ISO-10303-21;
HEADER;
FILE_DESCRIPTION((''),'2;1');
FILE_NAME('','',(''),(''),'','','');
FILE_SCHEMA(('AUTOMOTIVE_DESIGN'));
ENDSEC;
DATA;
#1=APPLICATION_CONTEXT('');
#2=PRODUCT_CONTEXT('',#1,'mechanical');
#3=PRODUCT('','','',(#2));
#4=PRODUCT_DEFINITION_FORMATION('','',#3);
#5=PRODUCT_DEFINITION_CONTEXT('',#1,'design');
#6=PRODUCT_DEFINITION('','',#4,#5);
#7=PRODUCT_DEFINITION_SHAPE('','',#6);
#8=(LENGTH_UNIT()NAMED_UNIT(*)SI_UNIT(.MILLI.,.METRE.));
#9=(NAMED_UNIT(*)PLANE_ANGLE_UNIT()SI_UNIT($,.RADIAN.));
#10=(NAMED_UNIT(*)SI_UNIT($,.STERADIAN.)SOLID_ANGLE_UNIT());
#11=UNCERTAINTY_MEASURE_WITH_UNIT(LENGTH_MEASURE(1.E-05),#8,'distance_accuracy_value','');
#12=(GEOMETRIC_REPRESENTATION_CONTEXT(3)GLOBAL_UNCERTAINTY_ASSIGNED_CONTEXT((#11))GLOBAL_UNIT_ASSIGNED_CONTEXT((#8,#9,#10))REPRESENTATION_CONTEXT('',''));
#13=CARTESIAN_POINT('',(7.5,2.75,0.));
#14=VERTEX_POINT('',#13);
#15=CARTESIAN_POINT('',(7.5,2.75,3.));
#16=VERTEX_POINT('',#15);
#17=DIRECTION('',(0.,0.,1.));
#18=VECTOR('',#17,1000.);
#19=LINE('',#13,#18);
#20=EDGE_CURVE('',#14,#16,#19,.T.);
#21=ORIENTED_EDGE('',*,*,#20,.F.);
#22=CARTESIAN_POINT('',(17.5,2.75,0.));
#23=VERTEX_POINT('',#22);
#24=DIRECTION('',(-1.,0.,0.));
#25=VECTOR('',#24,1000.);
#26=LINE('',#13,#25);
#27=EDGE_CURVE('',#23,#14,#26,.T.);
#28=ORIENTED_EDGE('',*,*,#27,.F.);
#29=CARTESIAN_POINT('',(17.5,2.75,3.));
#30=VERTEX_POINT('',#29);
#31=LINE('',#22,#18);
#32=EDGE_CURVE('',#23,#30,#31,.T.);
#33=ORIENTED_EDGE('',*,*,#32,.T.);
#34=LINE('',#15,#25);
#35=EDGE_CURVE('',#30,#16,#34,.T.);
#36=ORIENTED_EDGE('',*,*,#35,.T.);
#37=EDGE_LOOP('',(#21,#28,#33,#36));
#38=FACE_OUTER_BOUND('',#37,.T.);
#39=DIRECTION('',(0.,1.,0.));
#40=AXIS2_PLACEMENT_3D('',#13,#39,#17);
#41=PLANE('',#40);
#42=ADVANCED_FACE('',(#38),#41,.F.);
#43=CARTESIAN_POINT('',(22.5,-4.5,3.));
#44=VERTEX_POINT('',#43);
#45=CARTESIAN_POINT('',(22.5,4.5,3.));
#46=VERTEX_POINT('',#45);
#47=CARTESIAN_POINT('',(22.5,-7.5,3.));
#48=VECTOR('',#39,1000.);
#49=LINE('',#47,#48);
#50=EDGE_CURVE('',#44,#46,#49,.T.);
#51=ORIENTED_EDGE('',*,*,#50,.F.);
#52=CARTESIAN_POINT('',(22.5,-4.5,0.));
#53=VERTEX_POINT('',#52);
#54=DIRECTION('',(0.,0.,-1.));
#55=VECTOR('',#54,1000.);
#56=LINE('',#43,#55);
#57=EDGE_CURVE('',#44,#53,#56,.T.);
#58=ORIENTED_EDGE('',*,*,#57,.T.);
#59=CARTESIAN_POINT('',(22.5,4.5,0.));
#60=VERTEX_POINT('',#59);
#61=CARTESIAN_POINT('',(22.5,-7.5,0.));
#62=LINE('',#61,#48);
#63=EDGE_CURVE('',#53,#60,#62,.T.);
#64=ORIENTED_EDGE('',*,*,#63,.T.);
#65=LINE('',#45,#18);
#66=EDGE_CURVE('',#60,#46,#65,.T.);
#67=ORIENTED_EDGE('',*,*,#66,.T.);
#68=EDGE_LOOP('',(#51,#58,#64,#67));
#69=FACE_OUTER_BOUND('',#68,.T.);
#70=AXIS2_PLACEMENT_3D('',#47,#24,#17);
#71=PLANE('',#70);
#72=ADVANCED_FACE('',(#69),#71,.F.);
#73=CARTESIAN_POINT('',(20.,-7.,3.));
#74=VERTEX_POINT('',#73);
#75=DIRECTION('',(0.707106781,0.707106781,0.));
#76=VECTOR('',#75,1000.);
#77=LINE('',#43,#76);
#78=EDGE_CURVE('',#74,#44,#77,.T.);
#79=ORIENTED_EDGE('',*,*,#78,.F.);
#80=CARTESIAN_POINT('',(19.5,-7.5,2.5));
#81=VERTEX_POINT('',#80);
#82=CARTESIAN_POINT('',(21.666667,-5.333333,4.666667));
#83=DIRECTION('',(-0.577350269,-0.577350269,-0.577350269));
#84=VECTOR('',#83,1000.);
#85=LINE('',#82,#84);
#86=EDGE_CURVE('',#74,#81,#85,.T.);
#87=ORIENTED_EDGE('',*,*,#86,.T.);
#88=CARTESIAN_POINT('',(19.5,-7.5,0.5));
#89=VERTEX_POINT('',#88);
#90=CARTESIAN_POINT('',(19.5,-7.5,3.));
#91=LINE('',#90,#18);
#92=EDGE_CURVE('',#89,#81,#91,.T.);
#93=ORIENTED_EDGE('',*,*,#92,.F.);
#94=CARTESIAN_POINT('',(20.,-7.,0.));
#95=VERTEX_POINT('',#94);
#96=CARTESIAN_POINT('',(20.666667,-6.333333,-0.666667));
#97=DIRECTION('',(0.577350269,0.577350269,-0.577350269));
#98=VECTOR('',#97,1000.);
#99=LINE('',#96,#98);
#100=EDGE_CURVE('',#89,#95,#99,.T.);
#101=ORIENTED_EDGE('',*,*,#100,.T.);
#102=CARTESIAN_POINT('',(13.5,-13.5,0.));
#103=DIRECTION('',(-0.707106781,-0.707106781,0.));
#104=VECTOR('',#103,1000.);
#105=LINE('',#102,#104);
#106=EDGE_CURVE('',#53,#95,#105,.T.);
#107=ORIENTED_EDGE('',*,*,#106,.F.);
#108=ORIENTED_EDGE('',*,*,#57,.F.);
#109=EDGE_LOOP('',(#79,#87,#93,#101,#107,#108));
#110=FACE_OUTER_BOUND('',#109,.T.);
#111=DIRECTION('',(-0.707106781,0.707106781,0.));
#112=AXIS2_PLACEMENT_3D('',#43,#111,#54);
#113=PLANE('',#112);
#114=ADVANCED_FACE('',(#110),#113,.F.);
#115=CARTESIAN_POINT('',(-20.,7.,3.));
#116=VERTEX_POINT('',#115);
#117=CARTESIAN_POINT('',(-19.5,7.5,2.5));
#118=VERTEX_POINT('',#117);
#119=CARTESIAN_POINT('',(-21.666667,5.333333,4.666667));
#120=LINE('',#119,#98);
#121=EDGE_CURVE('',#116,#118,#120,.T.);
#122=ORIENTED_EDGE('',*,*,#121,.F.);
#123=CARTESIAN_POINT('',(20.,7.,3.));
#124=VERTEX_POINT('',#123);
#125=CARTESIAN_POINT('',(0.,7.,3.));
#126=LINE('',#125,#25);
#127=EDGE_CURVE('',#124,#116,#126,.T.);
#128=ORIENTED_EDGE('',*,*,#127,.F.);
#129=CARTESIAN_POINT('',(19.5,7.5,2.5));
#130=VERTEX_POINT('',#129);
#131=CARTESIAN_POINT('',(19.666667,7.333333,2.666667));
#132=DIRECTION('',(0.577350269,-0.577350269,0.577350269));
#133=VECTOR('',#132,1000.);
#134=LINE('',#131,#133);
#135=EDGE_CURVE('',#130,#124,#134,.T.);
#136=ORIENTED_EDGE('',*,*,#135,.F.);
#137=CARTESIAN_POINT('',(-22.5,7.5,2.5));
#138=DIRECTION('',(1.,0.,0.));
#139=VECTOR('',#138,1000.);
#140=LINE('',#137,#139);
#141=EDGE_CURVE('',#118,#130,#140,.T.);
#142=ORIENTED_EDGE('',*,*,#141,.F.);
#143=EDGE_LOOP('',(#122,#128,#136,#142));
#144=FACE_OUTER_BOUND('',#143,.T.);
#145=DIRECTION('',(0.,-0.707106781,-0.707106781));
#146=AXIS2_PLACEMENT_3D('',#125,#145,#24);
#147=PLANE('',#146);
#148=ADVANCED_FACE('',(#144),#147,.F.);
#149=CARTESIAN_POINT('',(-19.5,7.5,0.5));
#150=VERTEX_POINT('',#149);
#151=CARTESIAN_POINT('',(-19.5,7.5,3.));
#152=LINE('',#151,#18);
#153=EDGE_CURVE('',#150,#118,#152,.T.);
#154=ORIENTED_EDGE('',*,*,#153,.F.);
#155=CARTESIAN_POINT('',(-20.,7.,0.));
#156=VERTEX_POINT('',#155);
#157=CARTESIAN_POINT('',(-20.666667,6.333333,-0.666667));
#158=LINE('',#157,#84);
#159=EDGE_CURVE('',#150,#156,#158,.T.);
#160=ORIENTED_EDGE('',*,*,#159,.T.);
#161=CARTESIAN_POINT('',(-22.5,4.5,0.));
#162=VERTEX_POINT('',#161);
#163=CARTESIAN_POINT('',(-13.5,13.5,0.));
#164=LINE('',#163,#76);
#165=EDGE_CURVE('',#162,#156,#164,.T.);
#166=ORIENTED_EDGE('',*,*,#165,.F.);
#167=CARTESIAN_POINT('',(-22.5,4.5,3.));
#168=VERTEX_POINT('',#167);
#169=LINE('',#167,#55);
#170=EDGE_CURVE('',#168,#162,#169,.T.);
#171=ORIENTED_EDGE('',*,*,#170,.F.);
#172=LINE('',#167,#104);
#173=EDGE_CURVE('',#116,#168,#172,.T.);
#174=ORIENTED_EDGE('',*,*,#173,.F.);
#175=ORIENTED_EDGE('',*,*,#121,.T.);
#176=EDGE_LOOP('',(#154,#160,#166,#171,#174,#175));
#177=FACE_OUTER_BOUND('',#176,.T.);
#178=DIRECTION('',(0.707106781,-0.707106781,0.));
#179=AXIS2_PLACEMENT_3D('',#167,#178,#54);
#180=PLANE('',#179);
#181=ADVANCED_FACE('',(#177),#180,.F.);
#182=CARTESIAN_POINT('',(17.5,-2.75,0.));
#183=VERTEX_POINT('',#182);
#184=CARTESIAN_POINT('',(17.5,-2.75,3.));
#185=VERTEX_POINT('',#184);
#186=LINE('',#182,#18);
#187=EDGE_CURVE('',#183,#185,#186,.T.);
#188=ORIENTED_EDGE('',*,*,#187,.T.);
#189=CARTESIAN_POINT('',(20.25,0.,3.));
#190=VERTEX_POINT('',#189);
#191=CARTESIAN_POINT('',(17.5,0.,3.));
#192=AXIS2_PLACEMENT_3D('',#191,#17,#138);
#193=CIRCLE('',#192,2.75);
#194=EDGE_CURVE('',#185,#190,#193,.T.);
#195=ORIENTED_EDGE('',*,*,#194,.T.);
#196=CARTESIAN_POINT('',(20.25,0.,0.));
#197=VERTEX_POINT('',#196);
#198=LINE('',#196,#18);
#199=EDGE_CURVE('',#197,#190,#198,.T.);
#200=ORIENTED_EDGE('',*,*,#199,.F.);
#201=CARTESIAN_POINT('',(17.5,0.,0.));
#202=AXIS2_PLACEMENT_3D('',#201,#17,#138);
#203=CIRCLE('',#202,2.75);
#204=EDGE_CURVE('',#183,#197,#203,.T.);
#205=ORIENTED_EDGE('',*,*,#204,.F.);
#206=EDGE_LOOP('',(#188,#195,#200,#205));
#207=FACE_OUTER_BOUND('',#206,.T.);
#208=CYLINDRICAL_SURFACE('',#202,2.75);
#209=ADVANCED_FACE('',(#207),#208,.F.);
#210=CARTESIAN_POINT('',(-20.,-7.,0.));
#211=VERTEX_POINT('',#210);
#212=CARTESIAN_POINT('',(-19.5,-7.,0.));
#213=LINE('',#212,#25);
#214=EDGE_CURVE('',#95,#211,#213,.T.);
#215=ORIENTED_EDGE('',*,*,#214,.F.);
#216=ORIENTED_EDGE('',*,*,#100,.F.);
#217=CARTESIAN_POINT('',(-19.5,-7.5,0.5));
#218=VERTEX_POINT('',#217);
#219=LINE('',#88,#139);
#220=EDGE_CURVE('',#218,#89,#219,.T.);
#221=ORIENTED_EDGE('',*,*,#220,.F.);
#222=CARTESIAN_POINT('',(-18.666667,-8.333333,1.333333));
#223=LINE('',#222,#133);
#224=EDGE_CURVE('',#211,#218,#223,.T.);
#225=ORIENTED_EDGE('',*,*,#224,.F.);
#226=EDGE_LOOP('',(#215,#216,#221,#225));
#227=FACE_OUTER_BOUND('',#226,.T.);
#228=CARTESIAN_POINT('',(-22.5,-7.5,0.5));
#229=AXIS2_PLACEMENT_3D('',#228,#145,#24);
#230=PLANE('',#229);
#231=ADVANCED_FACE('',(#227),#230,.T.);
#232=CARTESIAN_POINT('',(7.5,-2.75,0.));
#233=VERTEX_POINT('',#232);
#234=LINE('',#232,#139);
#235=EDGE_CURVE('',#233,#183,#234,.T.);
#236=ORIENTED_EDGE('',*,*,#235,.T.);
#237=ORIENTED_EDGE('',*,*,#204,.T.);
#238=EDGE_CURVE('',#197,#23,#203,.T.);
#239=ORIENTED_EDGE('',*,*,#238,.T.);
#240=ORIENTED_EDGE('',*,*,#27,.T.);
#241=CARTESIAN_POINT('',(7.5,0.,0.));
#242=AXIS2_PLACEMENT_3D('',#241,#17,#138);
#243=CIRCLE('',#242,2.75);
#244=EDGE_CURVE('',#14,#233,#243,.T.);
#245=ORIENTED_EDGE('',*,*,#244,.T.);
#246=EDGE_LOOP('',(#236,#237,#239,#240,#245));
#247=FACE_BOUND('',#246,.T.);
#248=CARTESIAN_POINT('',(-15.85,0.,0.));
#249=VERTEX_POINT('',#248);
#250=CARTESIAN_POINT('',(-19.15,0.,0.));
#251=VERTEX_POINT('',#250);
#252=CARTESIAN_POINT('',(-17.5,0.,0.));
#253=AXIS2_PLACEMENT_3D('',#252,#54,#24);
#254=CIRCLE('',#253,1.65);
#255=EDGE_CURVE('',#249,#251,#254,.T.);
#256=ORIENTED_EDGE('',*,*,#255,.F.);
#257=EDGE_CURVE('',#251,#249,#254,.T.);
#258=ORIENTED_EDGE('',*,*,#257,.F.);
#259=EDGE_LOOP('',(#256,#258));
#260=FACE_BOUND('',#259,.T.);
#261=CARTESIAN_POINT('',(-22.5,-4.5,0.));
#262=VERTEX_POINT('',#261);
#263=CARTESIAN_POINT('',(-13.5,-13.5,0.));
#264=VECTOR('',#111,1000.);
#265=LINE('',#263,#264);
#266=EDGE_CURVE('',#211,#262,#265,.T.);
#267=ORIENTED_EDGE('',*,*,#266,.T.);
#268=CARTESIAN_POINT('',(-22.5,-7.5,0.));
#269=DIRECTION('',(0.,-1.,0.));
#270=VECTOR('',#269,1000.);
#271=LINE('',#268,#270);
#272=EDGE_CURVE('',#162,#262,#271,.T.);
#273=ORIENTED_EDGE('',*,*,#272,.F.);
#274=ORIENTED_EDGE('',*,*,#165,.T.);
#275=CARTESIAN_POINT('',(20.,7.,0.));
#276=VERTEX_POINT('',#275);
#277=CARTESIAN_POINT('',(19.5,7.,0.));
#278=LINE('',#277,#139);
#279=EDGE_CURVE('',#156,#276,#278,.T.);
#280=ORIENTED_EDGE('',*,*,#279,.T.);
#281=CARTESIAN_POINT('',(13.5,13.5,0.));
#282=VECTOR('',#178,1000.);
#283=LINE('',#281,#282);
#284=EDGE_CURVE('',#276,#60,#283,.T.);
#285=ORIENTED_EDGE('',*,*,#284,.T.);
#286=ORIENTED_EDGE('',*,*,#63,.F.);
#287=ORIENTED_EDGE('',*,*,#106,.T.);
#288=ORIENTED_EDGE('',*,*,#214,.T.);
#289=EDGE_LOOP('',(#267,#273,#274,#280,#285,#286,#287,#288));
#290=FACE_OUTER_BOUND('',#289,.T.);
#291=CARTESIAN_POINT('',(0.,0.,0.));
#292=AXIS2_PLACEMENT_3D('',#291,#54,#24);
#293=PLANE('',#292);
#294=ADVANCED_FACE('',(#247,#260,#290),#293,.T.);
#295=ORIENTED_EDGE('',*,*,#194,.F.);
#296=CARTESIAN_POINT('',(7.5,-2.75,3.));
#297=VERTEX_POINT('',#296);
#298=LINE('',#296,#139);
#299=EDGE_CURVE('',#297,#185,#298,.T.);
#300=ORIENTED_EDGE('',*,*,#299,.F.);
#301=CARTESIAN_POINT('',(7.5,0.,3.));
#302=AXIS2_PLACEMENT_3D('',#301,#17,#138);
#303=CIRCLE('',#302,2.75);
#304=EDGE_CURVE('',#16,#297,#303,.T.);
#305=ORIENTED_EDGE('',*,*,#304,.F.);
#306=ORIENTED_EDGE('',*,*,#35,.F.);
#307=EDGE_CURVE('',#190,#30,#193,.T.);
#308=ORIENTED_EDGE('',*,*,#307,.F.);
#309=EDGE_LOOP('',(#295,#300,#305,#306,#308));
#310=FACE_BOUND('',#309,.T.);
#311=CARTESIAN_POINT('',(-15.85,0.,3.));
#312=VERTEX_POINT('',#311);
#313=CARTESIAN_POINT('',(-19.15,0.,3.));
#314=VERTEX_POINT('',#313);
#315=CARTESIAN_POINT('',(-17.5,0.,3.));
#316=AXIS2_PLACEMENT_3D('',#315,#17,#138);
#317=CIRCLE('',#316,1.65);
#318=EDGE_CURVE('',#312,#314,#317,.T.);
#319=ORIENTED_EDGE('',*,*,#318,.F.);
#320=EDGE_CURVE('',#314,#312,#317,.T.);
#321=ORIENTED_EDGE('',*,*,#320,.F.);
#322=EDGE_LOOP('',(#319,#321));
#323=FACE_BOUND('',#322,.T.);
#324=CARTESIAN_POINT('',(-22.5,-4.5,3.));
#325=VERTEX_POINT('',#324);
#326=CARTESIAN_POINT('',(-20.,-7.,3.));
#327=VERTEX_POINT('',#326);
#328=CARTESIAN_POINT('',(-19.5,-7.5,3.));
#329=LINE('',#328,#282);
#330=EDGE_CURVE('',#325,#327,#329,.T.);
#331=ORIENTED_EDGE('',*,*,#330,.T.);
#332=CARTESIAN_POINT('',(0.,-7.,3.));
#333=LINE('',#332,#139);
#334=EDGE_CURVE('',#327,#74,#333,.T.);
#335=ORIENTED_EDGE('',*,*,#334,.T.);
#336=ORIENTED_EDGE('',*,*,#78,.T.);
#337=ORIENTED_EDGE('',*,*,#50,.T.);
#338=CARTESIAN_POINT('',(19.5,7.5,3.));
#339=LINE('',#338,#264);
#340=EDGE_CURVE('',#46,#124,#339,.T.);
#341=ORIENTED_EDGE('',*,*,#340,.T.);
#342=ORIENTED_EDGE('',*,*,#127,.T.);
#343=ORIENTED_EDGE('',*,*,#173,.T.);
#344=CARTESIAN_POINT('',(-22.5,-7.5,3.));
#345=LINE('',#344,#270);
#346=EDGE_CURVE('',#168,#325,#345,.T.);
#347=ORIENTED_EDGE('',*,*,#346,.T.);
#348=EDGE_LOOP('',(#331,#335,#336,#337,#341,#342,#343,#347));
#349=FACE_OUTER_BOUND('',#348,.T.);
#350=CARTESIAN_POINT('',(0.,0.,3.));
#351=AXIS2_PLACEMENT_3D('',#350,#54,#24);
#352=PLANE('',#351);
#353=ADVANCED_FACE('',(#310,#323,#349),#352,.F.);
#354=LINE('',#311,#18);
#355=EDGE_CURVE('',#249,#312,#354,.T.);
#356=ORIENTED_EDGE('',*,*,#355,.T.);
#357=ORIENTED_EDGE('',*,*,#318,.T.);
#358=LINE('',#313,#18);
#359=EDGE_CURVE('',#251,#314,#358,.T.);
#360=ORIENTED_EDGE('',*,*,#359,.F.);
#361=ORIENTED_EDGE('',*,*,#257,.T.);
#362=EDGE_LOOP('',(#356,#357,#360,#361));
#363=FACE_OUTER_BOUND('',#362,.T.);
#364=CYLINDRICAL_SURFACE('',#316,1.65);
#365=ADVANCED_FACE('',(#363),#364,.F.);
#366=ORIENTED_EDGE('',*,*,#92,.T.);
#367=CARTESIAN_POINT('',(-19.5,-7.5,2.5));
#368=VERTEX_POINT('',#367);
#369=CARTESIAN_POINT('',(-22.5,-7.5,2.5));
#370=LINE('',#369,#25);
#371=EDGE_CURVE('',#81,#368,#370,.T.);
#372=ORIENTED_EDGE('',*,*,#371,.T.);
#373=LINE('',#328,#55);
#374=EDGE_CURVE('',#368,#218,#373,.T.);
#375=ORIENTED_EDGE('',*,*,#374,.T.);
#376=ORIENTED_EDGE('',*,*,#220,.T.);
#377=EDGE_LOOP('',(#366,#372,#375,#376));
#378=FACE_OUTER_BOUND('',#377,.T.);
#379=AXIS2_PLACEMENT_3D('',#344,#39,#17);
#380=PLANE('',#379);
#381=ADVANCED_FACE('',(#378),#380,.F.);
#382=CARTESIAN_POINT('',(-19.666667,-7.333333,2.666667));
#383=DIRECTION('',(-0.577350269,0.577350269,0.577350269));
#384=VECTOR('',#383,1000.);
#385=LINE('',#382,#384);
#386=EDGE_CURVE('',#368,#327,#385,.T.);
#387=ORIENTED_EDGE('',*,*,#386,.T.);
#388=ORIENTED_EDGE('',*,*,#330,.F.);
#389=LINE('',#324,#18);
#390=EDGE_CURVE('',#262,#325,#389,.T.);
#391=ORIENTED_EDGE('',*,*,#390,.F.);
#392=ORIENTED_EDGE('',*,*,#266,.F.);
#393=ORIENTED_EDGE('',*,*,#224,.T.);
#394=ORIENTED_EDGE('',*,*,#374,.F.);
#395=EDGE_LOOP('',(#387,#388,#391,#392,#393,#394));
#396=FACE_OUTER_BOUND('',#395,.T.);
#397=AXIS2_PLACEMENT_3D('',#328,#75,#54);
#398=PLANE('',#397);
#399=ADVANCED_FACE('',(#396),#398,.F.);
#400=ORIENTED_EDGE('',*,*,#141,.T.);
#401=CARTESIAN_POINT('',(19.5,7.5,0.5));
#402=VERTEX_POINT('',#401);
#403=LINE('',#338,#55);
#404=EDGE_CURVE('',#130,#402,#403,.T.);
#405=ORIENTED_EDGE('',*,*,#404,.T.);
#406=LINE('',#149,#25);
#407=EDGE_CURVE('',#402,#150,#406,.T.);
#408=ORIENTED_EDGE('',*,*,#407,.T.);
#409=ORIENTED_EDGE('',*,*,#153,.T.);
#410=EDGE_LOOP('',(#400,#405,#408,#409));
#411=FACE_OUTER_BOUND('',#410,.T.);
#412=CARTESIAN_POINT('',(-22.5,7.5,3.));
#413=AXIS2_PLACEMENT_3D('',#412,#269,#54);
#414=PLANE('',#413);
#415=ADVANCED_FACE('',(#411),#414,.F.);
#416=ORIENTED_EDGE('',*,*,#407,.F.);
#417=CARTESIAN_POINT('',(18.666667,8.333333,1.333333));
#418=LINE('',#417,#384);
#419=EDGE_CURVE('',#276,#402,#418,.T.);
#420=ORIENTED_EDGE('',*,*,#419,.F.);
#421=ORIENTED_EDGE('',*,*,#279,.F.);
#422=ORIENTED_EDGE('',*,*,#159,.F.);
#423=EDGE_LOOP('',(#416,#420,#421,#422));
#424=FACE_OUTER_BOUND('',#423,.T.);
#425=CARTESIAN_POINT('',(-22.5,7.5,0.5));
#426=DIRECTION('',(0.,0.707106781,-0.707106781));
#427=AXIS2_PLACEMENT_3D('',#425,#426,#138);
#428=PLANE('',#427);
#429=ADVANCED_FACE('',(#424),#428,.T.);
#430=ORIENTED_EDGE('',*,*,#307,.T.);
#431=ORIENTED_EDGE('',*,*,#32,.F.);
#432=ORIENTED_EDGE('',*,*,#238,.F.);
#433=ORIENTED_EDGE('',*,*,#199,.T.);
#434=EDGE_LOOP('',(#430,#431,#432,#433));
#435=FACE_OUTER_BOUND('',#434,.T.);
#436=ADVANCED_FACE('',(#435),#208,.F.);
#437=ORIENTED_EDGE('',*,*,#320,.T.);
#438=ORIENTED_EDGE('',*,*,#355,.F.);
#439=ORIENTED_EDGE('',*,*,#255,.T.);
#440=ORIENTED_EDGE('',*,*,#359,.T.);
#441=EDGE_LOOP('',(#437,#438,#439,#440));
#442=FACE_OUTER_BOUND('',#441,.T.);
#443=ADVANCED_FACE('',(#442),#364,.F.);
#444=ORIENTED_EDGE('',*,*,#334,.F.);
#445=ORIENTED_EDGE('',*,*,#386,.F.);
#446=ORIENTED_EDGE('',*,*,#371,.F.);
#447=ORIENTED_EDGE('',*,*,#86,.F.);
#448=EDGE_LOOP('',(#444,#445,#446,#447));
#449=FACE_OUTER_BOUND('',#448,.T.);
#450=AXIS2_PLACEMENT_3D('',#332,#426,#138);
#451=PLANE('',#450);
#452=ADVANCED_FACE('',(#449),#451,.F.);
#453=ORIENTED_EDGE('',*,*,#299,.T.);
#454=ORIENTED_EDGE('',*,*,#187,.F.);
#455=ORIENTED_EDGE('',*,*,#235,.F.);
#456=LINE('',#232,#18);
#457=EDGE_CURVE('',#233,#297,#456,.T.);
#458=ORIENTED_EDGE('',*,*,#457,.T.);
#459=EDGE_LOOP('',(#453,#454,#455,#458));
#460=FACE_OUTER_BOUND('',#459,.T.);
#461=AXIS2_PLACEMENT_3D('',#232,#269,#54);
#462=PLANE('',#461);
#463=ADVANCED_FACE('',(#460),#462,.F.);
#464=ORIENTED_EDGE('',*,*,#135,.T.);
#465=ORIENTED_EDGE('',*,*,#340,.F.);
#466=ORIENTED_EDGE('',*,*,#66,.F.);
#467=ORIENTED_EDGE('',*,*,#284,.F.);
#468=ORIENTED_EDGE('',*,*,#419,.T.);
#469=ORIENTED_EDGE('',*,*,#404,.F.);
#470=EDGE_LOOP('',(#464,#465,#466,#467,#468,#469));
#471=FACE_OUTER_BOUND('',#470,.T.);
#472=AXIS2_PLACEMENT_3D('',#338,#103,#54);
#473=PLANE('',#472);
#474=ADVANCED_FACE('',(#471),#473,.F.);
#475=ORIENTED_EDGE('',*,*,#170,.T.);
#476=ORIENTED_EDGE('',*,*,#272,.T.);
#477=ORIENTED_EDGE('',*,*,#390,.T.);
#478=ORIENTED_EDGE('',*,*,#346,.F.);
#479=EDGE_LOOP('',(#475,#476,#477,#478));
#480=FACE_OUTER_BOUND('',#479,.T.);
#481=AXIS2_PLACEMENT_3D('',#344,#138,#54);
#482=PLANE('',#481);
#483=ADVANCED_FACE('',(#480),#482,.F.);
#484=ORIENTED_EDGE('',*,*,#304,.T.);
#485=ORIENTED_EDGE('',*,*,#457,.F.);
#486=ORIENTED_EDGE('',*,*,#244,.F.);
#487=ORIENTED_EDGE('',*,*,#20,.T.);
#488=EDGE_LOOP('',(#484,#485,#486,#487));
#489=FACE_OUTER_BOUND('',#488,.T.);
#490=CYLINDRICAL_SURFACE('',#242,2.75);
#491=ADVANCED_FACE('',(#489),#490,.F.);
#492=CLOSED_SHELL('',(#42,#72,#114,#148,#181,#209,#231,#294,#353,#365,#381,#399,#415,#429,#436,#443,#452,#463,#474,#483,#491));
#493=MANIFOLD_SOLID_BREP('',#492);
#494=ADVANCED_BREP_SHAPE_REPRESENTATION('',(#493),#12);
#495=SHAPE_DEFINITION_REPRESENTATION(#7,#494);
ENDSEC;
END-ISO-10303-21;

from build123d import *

# Parameters (mm, degrees)
SKETCH1_W             = 45
SKETCH1_H             = 15
BOSS_EXTRUDE1_DEPTH   = 3
M4_TAPPED_HOLE1_D     = 3.3
M4_TAPPED_HOLE1_DEPTH = 10.1
M4_TAPPED_HOLE1_TIP   = 0.991420021
CUT_EXTRUDE1_DEPTH    = 3
CHAMFER1_SIZE         = 3
CHAMFER2_SIZE         = 0.5


with BuildPart() as part:
    # Sketch1 → Boss-Extrude1 (new body)
    with BuildSketch(Plane.XY):
        Rectangle(SKETCH1_W, SKETCH1_H)
    extrude(amount=BOSS_EXTRUDE1_DEPTH)

    # M4 Tapped Hole1
    with Locations(Plane.XY.offset(3)):
        with Locations((-17.5, 0)):
            Hole(M4_TAPPED_HOLE1_D / 2, depth=M4_TAPPED_HOLE1_DEPTH)
            with Locations((0, 0, -(M4_TAPPED_HOLE1_DEPTH + M4_TAPPED_HOLE1_TIP / 2))):  # 118° drill point
                Cone(0, M4_TAPPED_HOLE1_D / 2, M4_TAPPED_HOLE1_TIP, mode=Mode.SUBTRACT)

    # Sketch4 → Cut-Extrude1 (cut)
    with BuildSketch(Plane.XY.offset(3)):
        with BuildLine():
            Line((7.5, 2.75), (17.5, 2.75))
            ThreePointArc((17.5, 2.75), (20.25, 0), (17.5, -2.75))
            Line((17.5, -2.75), (7.5, -2.75))
            ThreePointArc((7.5, -2.75), (4.75, 0), (7.5, 2.75))
        make_face()
    extrude(amount=-CUT_EXTRUDE1_DEPTH, mode=Mode.SUBTRACT)

    # Chamfer1
    chamfer1_edges = [part.edges().sort_by_distance(p)[0] for p in [
        (22.5, -7.5, 1.5),
        (-22.5, -7.5, 1.5),
        (-22.5, 7.5, 1.5),
        (22.5, 7.5, 1.5),
    ]]
    chamfer(chamfer1_edges, length=CHAMFER1_SIZE)

    # Chamfer2
    chamfer2_edges = [part.edges().sort_by_distance(p)[0] for p in [
        (0, -7.5, 0),
        (0, 7.5, 0),
        (0, -7.5, 3),
        (0, 7.5, 3),
    ]]
    chamfer(chamfer2_edges, length=CHAMFER2_SIZE)


solid = part.part
